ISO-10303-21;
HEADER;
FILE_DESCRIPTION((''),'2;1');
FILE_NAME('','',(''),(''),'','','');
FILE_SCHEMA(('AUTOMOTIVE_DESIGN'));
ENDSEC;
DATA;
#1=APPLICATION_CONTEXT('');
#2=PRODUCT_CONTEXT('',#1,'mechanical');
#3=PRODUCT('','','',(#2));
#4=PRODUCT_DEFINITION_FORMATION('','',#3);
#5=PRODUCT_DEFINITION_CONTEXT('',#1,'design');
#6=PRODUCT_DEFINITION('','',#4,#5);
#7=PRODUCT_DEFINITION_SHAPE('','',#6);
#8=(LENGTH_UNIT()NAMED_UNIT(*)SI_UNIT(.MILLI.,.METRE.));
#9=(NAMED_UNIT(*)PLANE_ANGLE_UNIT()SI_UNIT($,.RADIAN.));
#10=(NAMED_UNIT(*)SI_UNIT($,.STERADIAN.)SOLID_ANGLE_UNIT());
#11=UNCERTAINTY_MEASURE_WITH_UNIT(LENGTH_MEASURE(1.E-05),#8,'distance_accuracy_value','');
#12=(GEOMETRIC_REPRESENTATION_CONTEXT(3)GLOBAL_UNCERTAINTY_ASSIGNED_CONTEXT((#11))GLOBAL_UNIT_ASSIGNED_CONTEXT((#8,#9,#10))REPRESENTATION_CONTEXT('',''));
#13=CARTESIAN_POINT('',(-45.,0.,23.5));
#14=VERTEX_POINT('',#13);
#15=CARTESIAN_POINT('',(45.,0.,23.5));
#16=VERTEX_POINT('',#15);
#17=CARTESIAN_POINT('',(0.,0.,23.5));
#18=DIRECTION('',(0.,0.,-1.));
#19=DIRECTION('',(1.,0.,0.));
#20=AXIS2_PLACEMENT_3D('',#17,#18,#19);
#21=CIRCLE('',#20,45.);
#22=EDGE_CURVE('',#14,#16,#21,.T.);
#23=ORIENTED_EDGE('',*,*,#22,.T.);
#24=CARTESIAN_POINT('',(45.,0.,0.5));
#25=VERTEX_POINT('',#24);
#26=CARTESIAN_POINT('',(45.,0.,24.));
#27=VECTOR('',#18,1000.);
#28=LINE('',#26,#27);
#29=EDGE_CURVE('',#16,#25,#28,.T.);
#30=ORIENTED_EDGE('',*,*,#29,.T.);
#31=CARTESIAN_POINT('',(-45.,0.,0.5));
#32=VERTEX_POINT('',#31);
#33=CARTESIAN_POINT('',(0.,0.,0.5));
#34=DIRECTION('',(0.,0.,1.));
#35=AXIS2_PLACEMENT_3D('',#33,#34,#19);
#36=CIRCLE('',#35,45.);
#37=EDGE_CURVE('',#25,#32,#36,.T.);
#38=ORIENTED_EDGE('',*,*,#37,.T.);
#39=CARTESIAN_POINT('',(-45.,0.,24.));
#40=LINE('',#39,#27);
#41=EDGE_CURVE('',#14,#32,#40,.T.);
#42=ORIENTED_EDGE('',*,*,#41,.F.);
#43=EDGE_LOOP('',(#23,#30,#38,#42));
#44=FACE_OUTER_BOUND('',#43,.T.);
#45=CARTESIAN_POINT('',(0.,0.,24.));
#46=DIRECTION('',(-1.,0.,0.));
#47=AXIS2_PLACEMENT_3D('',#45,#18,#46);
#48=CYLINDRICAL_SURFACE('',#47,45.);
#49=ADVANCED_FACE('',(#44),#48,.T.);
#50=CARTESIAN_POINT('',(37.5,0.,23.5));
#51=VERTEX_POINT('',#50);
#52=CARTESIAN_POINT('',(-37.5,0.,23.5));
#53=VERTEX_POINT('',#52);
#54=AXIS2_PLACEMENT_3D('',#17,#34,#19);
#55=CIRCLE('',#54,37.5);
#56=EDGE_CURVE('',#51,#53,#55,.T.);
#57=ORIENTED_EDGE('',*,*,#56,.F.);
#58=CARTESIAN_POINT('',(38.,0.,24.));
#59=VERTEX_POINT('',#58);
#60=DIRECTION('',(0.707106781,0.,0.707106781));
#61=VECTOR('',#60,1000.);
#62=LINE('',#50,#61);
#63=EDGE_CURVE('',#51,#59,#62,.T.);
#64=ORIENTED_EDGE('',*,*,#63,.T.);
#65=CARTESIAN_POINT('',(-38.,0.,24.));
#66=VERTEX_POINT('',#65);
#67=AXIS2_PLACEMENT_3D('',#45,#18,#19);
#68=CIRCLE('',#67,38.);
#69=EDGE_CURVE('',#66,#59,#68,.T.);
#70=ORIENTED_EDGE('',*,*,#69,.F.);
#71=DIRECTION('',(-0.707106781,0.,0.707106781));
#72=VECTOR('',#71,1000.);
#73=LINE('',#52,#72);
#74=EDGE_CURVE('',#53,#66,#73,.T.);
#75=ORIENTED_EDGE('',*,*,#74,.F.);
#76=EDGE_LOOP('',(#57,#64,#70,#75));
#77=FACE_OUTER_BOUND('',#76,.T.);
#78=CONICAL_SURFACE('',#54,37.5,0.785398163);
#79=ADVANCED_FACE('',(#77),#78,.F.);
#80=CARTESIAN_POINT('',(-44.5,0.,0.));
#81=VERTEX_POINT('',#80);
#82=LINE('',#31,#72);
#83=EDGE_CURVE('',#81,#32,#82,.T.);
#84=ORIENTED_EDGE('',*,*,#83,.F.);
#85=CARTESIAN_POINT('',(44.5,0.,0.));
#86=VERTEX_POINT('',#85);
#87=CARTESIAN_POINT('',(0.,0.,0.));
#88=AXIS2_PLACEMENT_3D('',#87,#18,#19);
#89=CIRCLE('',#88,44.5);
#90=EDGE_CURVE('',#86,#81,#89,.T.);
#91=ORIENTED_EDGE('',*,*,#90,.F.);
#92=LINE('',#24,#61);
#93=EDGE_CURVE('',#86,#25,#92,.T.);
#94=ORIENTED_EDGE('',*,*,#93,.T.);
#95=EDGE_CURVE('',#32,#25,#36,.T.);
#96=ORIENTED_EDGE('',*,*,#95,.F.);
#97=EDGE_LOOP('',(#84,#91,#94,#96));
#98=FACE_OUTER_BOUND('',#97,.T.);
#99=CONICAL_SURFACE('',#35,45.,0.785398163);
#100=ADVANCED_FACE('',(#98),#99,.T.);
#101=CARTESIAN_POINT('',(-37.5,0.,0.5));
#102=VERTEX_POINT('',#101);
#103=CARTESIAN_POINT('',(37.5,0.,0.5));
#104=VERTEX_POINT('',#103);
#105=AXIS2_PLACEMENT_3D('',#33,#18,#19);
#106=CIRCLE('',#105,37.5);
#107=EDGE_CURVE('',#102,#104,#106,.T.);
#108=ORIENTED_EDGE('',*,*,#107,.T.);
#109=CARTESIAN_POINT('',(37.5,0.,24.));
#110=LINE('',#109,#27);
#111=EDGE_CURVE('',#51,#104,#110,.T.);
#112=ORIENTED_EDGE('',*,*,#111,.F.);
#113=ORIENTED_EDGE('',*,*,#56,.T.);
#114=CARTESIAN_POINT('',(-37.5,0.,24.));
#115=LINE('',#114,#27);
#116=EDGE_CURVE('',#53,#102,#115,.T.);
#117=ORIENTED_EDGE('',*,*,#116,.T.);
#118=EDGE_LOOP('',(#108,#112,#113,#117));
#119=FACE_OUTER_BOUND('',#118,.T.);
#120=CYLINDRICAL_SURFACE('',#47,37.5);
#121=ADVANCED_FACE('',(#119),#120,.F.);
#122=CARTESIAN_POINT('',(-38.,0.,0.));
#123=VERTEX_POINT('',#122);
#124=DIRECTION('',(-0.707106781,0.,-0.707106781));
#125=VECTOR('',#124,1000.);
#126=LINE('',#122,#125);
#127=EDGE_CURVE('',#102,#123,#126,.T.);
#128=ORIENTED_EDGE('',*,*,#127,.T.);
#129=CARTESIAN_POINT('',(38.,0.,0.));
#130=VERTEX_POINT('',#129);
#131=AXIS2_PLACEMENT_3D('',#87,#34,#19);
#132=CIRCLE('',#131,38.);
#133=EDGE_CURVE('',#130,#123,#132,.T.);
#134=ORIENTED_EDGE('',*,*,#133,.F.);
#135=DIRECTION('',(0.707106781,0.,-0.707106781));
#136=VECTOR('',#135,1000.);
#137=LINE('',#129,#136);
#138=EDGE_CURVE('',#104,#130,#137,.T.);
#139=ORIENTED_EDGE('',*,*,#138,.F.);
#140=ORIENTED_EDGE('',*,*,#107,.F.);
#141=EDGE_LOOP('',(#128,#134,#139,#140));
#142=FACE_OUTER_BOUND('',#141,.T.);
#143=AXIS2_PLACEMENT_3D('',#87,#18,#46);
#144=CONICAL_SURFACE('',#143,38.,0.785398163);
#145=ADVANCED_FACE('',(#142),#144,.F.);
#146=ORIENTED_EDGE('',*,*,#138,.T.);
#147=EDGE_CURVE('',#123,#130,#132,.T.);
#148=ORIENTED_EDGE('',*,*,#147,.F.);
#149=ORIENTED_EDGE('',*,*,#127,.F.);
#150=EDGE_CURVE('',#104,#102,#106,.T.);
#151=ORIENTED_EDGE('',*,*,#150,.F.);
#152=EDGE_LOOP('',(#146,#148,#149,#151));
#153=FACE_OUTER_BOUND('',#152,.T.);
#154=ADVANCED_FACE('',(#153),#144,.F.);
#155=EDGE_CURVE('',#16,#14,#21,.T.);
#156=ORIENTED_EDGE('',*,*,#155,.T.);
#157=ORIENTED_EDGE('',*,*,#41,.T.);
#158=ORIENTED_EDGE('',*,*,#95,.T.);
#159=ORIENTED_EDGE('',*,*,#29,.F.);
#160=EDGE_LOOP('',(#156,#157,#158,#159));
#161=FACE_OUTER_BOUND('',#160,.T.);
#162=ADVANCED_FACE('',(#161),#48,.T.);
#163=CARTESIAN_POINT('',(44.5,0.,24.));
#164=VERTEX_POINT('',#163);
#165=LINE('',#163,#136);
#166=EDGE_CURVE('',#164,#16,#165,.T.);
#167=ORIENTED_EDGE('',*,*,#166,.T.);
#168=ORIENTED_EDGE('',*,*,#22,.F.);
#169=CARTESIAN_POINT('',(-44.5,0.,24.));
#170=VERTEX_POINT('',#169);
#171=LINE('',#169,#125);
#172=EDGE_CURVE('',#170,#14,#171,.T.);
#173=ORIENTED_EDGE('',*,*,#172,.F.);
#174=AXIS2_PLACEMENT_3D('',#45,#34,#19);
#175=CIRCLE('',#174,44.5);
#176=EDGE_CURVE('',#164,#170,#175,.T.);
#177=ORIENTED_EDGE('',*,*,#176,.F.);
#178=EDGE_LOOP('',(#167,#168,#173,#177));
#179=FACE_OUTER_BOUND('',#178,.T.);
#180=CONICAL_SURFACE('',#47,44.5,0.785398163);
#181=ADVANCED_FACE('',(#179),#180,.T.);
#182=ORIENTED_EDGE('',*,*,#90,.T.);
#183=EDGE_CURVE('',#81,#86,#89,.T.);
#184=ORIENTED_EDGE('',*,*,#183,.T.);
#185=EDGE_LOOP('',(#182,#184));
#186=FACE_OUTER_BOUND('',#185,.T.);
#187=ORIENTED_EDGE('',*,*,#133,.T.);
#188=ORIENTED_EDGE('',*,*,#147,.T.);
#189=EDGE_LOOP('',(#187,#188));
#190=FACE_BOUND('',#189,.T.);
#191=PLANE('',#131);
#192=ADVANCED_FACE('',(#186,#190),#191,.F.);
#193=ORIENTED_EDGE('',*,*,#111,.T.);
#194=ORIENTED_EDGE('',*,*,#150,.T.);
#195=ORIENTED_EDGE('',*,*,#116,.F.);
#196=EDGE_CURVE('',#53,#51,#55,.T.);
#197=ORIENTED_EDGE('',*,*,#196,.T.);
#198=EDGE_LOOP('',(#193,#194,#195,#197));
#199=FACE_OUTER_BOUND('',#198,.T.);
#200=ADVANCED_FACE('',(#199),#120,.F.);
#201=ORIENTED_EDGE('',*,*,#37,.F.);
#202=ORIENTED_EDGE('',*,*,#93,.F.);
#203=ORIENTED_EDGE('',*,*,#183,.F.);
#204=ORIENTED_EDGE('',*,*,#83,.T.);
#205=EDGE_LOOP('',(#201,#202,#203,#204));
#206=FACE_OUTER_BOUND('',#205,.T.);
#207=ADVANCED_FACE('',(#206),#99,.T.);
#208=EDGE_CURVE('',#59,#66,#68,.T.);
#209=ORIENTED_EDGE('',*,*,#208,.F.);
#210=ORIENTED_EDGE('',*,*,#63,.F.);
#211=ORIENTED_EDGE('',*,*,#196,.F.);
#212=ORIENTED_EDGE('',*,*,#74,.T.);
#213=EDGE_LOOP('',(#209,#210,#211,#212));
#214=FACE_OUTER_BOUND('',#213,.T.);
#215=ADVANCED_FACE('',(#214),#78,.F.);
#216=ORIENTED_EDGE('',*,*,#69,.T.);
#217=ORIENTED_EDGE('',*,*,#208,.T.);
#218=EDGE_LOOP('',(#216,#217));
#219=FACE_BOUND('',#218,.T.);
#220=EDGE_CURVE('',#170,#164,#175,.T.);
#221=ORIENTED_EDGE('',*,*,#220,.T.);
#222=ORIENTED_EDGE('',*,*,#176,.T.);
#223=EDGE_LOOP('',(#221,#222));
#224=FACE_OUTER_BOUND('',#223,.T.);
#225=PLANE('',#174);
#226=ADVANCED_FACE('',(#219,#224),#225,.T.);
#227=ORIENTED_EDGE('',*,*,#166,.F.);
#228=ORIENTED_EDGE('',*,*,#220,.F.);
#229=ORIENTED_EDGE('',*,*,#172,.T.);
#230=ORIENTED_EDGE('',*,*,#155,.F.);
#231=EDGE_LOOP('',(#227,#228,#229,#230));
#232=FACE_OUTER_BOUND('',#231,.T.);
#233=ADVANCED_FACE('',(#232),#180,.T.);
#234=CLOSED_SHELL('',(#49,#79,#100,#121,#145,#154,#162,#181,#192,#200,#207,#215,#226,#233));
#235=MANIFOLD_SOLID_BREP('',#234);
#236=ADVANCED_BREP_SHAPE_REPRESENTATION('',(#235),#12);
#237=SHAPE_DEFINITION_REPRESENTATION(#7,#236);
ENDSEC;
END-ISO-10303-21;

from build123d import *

# Parameters (mm, degrees)
SKETCH1_R           = 45
SKETCH1_R_2         = 37.5
BOSS_EXTRUDE1_DEPTH = 24
CHAMFER1_SIZE       = 0.5


with BuildPart() as part:
    # Sketch1 → Boss-Extrude1 (new body)
    with BuildSketch(Plane.XY):
        Circle(SKETCH1_R)
        Circle(SKETCH1_R_2, mode=Mode.SUBTRACT)
    extrude(amount=BOSS_EXTRUDE1_DEPTH)

    # Chamfer1
    chamfer1_edges = [part.edges().sort_by_distance(p)[0] for p in [
        (-45, 0, 0),
        (-45, 0, 24),
        (-37.5, 0, 0),
        (-37.5, 0, 24),
    ]]
    chamfer(chamfer1_edges, length=CHAMFER1_SIZE)


solid = part.part
